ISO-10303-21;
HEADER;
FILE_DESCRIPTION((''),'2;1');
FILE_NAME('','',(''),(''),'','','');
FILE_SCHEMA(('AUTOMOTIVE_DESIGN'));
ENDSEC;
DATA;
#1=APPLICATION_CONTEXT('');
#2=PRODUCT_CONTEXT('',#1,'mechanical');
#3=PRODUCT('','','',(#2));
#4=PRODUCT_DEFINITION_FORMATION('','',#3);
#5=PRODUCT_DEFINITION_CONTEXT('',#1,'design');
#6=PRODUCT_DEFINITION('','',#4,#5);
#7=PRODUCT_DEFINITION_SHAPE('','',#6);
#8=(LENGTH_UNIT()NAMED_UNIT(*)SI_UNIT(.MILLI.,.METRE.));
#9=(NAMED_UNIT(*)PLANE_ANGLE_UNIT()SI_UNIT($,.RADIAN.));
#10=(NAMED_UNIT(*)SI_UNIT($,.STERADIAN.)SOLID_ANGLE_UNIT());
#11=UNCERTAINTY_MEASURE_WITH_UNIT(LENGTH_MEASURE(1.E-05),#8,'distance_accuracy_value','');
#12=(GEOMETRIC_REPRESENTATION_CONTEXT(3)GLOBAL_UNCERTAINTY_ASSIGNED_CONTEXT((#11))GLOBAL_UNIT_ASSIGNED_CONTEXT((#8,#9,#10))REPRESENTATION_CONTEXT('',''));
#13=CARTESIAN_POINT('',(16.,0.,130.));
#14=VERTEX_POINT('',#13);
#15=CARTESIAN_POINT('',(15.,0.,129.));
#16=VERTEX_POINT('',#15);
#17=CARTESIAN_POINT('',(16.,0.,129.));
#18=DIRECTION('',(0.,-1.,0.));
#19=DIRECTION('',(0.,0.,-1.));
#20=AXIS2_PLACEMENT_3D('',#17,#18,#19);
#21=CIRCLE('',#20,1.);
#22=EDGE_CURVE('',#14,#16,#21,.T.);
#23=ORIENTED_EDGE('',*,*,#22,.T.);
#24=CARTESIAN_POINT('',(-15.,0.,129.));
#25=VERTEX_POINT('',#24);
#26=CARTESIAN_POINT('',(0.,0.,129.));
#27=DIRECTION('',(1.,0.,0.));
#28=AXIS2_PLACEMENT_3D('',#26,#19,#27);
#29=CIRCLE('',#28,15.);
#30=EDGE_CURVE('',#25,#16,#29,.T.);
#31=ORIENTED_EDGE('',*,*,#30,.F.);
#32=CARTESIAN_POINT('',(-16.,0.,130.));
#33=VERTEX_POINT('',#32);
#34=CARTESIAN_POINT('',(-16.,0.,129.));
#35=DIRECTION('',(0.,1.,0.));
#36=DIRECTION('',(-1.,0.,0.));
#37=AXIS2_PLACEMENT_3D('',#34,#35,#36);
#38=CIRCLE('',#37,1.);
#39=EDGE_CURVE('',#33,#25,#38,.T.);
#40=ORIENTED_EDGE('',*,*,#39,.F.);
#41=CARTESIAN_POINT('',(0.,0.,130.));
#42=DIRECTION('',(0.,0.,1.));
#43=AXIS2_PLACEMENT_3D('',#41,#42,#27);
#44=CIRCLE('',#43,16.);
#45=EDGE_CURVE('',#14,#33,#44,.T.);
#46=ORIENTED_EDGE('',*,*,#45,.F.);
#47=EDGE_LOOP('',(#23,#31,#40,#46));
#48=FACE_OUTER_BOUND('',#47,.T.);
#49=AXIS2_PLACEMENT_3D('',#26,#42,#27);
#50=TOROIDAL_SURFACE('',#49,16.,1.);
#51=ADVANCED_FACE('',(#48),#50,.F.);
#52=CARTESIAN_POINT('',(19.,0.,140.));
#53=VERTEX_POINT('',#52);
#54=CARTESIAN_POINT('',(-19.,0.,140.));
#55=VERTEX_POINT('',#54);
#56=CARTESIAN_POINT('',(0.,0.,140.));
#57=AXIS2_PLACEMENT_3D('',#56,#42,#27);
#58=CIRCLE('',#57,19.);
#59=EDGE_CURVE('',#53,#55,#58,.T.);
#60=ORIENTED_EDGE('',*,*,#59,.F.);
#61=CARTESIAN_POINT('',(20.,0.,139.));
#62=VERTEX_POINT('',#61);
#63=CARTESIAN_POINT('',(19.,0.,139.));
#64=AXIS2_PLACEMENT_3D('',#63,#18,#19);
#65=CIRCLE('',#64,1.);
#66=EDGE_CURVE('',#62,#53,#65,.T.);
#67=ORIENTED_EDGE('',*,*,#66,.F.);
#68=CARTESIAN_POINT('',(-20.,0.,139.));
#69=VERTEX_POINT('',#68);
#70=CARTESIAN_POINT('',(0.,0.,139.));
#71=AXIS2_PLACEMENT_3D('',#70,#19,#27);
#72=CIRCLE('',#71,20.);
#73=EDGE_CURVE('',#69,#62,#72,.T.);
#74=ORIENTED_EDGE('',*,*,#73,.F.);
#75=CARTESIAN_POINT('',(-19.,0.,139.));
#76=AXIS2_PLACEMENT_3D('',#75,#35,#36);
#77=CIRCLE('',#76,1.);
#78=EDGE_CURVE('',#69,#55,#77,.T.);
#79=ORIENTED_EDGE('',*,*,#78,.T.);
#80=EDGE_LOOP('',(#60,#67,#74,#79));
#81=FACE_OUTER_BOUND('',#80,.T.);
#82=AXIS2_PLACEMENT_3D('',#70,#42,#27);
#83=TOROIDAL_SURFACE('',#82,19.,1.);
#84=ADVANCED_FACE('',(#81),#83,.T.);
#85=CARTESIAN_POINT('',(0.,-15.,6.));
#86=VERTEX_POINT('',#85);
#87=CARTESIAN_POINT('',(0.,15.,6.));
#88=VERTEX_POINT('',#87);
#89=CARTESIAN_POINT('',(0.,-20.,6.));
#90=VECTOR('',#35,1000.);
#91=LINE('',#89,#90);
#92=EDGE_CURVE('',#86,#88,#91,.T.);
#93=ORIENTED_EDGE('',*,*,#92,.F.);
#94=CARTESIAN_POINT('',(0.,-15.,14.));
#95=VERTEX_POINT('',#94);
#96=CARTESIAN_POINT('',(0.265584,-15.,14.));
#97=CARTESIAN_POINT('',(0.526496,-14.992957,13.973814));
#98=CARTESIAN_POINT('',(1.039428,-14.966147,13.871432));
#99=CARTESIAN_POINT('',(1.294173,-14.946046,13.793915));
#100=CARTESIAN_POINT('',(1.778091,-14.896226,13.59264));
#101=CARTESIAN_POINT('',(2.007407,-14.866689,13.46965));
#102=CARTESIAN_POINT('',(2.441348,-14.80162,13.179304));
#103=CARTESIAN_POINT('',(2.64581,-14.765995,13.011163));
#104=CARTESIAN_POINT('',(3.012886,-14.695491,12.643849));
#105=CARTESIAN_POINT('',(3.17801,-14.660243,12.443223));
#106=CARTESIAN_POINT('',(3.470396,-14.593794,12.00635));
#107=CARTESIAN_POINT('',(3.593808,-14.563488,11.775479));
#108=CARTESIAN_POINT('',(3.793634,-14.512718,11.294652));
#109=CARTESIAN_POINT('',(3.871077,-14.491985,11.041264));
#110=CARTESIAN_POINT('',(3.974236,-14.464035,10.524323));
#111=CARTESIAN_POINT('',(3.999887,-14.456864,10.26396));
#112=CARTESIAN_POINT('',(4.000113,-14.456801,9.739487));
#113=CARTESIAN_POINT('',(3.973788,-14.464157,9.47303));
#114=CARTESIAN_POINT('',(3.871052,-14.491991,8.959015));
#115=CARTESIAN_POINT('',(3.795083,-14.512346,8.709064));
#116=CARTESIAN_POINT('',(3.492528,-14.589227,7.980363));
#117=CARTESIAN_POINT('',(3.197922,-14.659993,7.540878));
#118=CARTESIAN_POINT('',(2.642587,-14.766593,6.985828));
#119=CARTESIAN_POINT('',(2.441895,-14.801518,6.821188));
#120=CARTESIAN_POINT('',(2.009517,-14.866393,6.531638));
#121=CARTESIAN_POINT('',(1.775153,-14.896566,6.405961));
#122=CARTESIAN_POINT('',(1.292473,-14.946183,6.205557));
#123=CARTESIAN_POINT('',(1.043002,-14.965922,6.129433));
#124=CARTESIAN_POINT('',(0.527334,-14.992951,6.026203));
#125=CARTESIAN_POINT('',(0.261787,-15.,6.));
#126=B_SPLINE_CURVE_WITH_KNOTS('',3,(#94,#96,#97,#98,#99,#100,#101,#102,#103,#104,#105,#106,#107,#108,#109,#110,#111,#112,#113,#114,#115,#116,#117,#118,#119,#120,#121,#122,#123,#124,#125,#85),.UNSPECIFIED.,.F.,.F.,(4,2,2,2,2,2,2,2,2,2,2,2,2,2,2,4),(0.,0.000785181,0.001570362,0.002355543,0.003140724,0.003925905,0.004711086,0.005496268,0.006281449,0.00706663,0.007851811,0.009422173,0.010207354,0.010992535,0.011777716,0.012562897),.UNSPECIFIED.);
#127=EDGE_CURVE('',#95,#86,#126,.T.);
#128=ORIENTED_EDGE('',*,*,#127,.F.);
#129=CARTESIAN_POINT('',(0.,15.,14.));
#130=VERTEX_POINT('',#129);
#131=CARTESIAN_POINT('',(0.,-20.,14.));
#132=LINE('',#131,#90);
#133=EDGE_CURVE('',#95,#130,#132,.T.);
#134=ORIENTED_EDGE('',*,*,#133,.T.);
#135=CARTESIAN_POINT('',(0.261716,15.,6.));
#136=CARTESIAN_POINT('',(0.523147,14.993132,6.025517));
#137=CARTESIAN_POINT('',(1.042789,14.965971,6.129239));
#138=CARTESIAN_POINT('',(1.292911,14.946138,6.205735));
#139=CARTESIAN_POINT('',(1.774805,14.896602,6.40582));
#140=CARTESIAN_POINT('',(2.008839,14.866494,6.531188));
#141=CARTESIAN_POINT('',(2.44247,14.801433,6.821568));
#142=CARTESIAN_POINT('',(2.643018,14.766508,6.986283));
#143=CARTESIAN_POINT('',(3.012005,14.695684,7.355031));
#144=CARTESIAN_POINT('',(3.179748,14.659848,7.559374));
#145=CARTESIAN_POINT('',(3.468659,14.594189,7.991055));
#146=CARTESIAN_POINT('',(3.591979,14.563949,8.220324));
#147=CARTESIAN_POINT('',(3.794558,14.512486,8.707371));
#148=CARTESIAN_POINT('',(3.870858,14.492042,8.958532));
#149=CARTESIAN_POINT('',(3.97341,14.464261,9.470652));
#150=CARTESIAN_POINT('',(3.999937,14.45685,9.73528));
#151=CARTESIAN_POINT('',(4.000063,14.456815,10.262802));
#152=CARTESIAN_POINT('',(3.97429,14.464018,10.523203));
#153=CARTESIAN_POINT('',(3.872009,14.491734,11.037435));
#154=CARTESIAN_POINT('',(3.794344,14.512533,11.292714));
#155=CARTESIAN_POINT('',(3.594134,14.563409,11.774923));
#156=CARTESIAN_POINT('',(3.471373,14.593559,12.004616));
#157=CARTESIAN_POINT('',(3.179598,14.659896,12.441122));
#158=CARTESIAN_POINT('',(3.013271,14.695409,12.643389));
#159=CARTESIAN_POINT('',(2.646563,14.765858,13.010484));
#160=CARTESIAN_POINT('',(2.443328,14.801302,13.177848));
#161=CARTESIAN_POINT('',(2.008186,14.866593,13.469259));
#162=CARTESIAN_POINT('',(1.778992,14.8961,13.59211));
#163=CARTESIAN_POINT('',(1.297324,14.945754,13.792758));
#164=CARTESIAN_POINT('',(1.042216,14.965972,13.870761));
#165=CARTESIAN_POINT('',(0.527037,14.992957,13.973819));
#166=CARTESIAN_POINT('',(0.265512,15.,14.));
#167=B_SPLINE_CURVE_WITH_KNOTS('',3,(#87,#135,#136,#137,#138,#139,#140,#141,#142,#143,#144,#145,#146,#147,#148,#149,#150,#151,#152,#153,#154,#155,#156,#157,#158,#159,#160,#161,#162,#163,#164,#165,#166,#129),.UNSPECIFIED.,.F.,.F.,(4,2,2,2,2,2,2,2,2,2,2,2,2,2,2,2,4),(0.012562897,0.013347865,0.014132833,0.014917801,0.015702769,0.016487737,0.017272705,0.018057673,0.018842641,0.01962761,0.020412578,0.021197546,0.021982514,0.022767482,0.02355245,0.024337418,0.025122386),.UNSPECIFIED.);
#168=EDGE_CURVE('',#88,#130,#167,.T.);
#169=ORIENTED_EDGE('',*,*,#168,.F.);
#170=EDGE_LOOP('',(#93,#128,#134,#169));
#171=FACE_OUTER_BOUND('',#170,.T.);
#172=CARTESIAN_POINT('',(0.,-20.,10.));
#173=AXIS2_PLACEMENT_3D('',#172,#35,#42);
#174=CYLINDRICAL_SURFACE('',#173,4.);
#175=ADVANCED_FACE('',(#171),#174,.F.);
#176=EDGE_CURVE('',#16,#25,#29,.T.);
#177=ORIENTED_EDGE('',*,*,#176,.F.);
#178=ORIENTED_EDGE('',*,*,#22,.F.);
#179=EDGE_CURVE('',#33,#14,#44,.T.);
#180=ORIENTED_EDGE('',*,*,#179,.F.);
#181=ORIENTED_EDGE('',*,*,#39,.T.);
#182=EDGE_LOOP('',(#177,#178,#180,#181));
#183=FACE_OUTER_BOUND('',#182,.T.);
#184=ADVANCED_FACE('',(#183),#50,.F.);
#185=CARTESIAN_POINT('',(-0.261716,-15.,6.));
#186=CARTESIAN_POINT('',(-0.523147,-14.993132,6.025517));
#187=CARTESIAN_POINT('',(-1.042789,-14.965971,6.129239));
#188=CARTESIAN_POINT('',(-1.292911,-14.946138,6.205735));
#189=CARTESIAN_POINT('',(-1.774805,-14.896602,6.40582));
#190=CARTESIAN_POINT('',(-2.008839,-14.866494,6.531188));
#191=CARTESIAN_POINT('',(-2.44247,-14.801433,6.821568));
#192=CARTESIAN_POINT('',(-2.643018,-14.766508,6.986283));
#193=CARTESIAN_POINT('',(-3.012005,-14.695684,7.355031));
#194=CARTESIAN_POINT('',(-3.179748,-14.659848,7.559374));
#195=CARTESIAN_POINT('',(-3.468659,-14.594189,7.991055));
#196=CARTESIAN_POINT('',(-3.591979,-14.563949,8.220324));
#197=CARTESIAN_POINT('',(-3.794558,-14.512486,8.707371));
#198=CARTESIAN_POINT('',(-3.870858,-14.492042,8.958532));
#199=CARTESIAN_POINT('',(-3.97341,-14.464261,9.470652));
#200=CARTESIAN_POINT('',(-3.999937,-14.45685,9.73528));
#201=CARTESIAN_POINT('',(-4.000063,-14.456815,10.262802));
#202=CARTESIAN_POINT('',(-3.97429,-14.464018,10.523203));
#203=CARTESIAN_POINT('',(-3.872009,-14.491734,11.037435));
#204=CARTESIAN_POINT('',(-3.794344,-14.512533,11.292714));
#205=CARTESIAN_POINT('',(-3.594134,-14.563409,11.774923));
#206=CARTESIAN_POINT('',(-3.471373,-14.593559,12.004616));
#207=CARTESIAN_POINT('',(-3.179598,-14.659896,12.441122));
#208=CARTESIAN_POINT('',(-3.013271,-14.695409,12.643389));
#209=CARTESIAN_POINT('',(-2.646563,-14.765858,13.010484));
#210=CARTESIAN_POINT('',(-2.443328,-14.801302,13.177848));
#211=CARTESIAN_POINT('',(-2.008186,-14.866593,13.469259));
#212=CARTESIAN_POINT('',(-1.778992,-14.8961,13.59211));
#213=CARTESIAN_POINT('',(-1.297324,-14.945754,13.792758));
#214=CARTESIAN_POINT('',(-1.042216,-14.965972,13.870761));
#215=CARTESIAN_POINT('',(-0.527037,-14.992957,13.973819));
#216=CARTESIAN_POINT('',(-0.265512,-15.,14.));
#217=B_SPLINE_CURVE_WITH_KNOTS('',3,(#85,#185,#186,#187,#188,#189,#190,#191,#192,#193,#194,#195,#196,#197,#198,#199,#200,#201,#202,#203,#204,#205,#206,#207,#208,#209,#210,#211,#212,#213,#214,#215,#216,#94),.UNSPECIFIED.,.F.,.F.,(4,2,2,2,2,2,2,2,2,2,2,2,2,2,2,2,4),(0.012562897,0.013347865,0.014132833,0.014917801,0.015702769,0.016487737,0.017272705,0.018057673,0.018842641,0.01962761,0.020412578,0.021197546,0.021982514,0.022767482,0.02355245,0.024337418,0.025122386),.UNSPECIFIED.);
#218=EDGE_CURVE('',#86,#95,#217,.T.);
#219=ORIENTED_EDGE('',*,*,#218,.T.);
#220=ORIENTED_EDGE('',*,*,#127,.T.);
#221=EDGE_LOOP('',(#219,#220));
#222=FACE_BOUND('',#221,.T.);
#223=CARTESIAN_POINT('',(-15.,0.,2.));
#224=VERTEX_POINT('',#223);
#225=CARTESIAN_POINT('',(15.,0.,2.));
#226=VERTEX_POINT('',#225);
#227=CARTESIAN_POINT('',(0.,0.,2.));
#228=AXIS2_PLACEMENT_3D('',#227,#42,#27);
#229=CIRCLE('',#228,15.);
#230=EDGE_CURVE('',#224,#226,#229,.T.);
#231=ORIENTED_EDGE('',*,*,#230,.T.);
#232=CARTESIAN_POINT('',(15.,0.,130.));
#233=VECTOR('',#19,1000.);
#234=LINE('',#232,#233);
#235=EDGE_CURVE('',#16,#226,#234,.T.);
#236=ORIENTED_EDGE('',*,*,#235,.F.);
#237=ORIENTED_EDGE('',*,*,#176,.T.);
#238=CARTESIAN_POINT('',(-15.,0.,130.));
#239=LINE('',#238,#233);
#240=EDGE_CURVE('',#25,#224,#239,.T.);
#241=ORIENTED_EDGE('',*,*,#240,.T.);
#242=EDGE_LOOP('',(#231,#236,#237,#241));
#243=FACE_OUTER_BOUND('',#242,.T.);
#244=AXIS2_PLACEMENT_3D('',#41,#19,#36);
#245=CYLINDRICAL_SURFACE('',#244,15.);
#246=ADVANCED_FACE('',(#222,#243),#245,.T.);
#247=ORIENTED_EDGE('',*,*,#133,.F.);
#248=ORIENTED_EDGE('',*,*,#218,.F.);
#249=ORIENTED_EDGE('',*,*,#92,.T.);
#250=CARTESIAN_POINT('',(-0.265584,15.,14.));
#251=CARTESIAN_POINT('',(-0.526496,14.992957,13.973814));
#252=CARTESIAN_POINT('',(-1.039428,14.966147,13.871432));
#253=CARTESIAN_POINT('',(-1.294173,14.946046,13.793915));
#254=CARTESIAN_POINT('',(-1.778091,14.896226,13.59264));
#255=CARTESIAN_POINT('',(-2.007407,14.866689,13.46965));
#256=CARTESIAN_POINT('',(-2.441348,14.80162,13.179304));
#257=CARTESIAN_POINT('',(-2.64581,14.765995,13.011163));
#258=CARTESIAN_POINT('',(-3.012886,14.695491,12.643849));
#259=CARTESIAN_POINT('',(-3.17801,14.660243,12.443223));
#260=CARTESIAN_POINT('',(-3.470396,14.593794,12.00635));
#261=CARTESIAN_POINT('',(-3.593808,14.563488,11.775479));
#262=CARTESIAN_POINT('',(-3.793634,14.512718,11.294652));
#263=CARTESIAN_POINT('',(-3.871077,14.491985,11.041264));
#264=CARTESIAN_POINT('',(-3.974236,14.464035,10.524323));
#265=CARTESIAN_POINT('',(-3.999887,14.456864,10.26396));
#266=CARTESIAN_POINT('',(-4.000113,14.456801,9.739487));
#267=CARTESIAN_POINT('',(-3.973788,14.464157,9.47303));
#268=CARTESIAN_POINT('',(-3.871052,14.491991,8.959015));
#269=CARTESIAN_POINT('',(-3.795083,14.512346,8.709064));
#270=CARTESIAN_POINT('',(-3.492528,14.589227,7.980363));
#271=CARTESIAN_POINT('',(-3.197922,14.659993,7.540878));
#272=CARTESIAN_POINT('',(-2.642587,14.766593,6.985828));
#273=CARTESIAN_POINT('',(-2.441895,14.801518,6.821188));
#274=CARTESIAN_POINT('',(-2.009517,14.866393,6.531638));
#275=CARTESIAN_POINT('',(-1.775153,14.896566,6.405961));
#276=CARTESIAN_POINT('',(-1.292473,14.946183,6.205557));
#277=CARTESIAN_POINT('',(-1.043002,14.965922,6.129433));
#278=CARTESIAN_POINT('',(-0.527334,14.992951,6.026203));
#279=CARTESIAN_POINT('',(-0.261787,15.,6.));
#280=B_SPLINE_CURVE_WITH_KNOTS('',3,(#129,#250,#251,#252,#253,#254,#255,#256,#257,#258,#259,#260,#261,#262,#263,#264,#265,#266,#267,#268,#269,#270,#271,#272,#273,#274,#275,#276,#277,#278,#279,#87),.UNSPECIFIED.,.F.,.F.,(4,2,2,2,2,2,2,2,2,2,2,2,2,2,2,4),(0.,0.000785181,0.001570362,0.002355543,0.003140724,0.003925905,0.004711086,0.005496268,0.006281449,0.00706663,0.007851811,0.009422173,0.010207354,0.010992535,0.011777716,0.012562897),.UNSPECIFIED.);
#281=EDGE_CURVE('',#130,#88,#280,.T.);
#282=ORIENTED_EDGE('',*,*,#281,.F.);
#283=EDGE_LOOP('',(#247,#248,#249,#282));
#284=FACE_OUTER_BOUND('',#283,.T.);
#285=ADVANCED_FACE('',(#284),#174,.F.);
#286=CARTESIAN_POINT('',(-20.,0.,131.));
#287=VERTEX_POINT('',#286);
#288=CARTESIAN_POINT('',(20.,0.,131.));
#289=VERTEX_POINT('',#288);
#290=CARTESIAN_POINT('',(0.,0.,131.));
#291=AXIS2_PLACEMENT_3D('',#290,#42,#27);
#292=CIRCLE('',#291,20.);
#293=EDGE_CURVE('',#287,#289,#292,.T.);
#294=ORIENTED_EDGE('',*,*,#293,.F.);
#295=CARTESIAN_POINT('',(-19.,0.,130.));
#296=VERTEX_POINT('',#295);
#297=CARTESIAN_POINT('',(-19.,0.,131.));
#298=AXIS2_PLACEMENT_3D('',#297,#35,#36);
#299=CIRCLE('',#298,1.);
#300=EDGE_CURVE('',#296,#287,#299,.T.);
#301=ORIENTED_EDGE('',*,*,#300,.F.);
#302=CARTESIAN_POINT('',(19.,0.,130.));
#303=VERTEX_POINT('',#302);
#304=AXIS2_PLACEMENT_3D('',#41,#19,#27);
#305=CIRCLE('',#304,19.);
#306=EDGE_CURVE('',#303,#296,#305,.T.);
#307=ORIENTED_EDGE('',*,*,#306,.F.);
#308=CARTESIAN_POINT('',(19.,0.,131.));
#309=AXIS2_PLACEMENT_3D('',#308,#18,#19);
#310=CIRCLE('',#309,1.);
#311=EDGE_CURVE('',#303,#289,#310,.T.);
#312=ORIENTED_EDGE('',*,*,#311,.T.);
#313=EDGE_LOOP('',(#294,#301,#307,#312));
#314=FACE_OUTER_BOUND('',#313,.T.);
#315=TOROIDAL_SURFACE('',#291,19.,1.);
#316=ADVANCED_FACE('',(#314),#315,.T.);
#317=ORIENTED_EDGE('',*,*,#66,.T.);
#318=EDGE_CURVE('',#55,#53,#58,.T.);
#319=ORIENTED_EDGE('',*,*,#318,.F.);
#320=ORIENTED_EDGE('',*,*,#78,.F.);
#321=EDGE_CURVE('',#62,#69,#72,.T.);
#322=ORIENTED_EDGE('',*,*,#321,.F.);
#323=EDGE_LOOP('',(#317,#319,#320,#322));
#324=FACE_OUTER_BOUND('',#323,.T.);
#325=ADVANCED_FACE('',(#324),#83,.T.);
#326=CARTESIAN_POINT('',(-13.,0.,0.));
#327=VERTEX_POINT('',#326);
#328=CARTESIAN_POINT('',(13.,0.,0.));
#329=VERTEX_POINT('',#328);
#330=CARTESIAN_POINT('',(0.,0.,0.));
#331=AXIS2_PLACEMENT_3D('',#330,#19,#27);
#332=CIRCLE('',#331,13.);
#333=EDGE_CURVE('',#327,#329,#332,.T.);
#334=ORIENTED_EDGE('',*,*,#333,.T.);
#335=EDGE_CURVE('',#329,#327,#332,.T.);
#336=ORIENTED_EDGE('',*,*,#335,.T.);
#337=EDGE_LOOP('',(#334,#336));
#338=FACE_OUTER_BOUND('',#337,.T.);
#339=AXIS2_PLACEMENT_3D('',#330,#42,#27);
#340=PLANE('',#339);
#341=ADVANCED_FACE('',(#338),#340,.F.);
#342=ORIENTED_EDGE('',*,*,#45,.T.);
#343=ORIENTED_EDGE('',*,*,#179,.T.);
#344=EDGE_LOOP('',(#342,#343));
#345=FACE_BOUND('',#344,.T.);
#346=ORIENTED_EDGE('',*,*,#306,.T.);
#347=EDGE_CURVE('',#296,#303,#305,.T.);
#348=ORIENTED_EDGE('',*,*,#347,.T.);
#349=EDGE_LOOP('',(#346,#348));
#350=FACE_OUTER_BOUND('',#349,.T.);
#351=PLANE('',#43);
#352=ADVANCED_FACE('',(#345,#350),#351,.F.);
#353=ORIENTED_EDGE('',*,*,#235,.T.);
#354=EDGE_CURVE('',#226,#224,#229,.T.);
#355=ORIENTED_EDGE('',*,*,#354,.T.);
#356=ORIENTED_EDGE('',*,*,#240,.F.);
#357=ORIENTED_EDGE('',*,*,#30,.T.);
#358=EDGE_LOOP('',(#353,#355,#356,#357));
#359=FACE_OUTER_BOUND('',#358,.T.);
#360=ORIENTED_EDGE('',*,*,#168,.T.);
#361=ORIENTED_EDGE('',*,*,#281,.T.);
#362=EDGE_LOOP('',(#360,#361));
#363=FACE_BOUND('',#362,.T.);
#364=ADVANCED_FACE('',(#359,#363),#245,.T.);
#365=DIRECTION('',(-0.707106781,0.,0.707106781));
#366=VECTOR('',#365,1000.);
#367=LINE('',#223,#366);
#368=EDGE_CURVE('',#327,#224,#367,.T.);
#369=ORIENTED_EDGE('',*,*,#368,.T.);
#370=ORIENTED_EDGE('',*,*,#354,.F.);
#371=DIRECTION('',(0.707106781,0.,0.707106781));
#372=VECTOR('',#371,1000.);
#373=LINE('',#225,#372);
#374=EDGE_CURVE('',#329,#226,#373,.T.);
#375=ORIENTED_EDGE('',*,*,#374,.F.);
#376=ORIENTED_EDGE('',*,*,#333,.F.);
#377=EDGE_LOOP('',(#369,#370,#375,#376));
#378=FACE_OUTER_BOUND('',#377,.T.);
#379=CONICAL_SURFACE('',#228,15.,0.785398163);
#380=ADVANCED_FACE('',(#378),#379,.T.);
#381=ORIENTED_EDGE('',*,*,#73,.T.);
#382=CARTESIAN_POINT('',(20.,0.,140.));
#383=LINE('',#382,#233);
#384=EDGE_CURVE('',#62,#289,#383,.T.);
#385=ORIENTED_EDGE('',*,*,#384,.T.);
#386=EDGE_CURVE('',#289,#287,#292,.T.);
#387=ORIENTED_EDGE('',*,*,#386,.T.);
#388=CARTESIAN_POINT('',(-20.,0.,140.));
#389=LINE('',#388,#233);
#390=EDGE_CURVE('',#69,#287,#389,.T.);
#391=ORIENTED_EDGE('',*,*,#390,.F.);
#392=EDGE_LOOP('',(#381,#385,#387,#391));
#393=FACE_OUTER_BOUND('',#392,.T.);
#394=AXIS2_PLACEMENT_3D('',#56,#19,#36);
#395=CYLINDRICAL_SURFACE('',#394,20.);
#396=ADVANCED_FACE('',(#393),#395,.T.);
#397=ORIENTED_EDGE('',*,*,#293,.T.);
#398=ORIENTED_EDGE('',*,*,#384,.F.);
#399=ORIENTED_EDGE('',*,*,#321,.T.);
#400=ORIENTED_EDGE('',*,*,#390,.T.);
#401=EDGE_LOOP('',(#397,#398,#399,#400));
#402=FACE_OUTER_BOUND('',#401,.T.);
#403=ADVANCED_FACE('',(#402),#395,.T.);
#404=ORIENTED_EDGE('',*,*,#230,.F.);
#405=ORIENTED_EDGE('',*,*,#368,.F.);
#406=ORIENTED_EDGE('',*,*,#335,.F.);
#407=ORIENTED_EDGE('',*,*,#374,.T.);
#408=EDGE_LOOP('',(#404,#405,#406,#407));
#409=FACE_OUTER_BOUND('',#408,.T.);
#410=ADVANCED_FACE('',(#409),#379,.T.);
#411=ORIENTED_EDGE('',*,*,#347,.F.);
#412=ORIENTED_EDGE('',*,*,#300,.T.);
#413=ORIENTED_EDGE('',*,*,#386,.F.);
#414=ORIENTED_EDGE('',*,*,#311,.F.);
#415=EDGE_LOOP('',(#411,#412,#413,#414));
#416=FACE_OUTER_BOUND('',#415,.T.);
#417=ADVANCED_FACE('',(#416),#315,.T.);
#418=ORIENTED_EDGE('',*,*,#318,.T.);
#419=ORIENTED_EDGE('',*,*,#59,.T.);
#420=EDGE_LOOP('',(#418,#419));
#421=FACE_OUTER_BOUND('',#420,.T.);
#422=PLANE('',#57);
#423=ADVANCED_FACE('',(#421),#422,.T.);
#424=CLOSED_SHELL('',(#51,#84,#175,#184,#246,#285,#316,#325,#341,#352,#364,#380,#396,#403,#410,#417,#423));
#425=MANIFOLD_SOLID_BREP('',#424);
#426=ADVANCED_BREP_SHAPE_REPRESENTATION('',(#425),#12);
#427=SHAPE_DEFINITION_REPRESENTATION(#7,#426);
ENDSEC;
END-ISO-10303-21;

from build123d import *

# Parameters (mm, degrees)
SKETCH1_R               = 15
BOSS_EXTRUDE1_DEPTH     = 130
SKETCH2_R               = 20
BOSS_EXTRUDE2_DEPTH     = 10
CUT_EXTRUDE1_DEPTH      = 143.828568571
CUT_EXTRUDE1_DEPTH_BACK = 143.828568571
SKETCH3_R               = 4
CHAMFER1_SIZE           = 2
FILLET1_R               = 1
FILLET2_R               = 1


with BuildPart() as part:
    # Sketch1 → Boss-Extrude1 (new body)
    with BuildSketch(Plane.XY):
        Circle(SKETCH1_R)
    extrude(amount=BOSS_EXTRUDE1_DEPTH)

    # Sketch2 → Boss-Extrude2 (add)
    with BuildSketch(Plane.XY.offset(130)):
        Circle(SKETCH2_R)
    extrude(amount=BOSS_EXTRUDE2_DEPTH)

    # Sketch3 → Cut-Extrude1 (cut, two sides: drawn at the far end of the back side and taken through both)
    with BuildSketch(Plane(origin=(0, 0, 0), x_dir=(1, 0, 0), z_dir=(0, 1, 0)).offset(-CUT_EXTRUDE1_DEPTH_BACK)):
        with Locations(Location((0, -10, 0), (0, 0, 270))):
            Circle(SKETCH3_R)
    extrude(amount=CUT_EXTRUDE1_DEPTH + CUT_EXTRUDE1_DEPTH_BACK, mode=Mode.SUBTRACT)

    # Chamfer1
    chamfer1_edges = [part.edges().sort_by_distance(p)[0] for p in [
        (-15, 0, 0),
    ]]
    chamfer(chamfer1_edges, length=CHAMFER1_SIZE)

    # Fillet1
    fillet1_edges = [part.edges().sort_by_distance(p)[0] for p in [
        (-15, 0, 130),
    ]]
    fillet(fillet1_edges, radius=FILLET1_R)

    # Fillet2
    fillet2_edges = [part.edges().sort_by_distance(p)[0] for p in [
        (-20, 0, 130),
        (-20, 0, 140),
    ]]
    fillet(fillet2_edges, radius=FILLET2_R)


solid = part.part
